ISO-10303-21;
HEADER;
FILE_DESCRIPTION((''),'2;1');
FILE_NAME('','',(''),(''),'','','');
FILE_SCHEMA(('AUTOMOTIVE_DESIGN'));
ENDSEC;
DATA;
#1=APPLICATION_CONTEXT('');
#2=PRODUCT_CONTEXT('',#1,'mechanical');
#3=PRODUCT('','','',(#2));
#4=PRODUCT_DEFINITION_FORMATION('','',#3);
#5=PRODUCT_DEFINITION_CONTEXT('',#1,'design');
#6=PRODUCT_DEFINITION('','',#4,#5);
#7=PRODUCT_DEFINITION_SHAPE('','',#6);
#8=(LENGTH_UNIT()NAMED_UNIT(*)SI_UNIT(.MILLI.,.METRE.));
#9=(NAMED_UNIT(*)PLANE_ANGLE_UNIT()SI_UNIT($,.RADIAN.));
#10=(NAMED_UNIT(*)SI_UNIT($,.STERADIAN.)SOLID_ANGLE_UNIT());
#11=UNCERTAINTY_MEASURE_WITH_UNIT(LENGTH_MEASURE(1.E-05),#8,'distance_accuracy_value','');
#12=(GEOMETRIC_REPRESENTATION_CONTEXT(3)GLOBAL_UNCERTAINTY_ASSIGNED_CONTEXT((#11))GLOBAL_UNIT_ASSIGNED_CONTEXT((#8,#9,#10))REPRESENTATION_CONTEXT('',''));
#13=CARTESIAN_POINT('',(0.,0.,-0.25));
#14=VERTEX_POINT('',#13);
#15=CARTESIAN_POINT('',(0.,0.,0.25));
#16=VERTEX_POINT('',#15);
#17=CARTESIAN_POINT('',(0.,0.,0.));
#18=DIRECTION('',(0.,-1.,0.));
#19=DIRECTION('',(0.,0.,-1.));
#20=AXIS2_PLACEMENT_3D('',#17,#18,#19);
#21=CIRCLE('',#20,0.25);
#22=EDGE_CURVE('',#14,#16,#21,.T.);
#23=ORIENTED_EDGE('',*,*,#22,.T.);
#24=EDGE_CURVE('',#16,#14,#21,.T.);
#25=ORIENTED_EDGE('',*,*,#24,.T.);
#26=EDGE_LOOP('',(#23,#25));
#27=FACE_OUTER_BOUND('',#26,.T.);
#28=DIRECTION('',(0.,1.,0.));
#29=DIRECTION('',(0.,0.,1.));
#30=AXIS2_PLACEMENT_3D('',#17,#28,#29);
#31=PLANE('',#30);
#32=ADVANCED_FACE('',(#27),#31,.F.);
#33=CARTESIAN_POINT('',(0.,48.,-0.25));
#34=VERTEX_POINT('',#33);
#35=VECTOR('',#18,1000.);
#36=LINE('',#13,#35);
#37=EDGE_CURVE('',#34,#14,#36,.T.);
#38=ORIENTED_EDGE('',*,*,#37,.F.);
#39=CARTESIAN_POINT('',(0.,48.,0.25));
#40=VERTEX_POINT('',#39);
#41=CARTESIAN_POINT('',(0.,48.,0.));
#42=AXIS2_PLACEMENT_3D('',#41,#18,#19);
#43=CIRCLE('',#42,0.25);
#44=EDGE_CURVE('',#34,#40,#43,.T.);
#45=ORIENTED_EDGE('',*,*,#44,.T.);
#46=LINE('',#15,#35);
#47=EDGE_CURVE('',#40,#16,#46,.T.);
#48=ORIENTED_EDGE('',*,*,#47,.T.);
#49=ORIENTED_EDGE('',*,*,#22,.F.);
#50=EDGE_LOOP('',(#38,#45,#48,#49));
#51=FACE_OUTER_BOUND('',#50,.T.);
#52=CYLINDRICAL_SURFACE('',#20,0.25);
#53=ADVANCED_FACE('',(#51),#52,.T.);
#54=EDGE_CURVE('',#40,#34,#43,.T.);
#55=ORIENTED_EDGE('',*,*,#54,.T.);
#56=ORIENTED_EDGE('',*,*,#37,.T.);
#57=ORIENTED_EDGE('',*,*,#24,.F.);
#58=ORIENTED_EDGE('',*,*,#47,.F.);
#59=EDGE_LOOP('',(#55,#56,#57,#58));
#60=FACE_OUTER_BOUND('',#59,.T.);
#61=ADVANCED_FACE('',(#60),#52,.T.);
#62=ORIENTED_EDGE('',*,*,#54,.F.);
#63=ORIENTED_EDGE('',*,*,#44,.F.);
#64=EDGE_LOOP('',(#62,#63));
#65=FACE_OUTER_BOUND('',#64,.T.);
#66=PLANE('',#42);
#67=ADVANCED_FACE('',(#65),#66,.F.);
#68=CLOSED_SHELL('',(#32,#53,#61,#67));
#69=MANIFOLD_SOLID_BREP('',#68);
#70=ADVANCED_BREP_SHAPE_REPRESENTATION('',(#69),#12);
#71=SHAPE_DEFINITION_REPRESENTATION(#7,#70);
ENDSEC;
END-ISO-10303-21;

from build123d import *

# Parameters (mm, degrees)
SKETCH1_W = 0.25
SKETCH1_H = 48


with BuildPart() as part:
    # Sketch1 → Revolve1 (revolve)
    with BuildSketch(Plane.XY, mode=Mode.PRIVATE) as revolve1_sk:
        with Locations((-0.125, 24)):
            Rectangle(SKETCH1_W, SKETCH1_H)
    revolve(revolve1_sk.sketch.rotate(Axis((0, 0, 0), (0, 1, 0)), 270), axis=Axis((0, 0, 0), (0, 1, 0)))


solid = part.part
